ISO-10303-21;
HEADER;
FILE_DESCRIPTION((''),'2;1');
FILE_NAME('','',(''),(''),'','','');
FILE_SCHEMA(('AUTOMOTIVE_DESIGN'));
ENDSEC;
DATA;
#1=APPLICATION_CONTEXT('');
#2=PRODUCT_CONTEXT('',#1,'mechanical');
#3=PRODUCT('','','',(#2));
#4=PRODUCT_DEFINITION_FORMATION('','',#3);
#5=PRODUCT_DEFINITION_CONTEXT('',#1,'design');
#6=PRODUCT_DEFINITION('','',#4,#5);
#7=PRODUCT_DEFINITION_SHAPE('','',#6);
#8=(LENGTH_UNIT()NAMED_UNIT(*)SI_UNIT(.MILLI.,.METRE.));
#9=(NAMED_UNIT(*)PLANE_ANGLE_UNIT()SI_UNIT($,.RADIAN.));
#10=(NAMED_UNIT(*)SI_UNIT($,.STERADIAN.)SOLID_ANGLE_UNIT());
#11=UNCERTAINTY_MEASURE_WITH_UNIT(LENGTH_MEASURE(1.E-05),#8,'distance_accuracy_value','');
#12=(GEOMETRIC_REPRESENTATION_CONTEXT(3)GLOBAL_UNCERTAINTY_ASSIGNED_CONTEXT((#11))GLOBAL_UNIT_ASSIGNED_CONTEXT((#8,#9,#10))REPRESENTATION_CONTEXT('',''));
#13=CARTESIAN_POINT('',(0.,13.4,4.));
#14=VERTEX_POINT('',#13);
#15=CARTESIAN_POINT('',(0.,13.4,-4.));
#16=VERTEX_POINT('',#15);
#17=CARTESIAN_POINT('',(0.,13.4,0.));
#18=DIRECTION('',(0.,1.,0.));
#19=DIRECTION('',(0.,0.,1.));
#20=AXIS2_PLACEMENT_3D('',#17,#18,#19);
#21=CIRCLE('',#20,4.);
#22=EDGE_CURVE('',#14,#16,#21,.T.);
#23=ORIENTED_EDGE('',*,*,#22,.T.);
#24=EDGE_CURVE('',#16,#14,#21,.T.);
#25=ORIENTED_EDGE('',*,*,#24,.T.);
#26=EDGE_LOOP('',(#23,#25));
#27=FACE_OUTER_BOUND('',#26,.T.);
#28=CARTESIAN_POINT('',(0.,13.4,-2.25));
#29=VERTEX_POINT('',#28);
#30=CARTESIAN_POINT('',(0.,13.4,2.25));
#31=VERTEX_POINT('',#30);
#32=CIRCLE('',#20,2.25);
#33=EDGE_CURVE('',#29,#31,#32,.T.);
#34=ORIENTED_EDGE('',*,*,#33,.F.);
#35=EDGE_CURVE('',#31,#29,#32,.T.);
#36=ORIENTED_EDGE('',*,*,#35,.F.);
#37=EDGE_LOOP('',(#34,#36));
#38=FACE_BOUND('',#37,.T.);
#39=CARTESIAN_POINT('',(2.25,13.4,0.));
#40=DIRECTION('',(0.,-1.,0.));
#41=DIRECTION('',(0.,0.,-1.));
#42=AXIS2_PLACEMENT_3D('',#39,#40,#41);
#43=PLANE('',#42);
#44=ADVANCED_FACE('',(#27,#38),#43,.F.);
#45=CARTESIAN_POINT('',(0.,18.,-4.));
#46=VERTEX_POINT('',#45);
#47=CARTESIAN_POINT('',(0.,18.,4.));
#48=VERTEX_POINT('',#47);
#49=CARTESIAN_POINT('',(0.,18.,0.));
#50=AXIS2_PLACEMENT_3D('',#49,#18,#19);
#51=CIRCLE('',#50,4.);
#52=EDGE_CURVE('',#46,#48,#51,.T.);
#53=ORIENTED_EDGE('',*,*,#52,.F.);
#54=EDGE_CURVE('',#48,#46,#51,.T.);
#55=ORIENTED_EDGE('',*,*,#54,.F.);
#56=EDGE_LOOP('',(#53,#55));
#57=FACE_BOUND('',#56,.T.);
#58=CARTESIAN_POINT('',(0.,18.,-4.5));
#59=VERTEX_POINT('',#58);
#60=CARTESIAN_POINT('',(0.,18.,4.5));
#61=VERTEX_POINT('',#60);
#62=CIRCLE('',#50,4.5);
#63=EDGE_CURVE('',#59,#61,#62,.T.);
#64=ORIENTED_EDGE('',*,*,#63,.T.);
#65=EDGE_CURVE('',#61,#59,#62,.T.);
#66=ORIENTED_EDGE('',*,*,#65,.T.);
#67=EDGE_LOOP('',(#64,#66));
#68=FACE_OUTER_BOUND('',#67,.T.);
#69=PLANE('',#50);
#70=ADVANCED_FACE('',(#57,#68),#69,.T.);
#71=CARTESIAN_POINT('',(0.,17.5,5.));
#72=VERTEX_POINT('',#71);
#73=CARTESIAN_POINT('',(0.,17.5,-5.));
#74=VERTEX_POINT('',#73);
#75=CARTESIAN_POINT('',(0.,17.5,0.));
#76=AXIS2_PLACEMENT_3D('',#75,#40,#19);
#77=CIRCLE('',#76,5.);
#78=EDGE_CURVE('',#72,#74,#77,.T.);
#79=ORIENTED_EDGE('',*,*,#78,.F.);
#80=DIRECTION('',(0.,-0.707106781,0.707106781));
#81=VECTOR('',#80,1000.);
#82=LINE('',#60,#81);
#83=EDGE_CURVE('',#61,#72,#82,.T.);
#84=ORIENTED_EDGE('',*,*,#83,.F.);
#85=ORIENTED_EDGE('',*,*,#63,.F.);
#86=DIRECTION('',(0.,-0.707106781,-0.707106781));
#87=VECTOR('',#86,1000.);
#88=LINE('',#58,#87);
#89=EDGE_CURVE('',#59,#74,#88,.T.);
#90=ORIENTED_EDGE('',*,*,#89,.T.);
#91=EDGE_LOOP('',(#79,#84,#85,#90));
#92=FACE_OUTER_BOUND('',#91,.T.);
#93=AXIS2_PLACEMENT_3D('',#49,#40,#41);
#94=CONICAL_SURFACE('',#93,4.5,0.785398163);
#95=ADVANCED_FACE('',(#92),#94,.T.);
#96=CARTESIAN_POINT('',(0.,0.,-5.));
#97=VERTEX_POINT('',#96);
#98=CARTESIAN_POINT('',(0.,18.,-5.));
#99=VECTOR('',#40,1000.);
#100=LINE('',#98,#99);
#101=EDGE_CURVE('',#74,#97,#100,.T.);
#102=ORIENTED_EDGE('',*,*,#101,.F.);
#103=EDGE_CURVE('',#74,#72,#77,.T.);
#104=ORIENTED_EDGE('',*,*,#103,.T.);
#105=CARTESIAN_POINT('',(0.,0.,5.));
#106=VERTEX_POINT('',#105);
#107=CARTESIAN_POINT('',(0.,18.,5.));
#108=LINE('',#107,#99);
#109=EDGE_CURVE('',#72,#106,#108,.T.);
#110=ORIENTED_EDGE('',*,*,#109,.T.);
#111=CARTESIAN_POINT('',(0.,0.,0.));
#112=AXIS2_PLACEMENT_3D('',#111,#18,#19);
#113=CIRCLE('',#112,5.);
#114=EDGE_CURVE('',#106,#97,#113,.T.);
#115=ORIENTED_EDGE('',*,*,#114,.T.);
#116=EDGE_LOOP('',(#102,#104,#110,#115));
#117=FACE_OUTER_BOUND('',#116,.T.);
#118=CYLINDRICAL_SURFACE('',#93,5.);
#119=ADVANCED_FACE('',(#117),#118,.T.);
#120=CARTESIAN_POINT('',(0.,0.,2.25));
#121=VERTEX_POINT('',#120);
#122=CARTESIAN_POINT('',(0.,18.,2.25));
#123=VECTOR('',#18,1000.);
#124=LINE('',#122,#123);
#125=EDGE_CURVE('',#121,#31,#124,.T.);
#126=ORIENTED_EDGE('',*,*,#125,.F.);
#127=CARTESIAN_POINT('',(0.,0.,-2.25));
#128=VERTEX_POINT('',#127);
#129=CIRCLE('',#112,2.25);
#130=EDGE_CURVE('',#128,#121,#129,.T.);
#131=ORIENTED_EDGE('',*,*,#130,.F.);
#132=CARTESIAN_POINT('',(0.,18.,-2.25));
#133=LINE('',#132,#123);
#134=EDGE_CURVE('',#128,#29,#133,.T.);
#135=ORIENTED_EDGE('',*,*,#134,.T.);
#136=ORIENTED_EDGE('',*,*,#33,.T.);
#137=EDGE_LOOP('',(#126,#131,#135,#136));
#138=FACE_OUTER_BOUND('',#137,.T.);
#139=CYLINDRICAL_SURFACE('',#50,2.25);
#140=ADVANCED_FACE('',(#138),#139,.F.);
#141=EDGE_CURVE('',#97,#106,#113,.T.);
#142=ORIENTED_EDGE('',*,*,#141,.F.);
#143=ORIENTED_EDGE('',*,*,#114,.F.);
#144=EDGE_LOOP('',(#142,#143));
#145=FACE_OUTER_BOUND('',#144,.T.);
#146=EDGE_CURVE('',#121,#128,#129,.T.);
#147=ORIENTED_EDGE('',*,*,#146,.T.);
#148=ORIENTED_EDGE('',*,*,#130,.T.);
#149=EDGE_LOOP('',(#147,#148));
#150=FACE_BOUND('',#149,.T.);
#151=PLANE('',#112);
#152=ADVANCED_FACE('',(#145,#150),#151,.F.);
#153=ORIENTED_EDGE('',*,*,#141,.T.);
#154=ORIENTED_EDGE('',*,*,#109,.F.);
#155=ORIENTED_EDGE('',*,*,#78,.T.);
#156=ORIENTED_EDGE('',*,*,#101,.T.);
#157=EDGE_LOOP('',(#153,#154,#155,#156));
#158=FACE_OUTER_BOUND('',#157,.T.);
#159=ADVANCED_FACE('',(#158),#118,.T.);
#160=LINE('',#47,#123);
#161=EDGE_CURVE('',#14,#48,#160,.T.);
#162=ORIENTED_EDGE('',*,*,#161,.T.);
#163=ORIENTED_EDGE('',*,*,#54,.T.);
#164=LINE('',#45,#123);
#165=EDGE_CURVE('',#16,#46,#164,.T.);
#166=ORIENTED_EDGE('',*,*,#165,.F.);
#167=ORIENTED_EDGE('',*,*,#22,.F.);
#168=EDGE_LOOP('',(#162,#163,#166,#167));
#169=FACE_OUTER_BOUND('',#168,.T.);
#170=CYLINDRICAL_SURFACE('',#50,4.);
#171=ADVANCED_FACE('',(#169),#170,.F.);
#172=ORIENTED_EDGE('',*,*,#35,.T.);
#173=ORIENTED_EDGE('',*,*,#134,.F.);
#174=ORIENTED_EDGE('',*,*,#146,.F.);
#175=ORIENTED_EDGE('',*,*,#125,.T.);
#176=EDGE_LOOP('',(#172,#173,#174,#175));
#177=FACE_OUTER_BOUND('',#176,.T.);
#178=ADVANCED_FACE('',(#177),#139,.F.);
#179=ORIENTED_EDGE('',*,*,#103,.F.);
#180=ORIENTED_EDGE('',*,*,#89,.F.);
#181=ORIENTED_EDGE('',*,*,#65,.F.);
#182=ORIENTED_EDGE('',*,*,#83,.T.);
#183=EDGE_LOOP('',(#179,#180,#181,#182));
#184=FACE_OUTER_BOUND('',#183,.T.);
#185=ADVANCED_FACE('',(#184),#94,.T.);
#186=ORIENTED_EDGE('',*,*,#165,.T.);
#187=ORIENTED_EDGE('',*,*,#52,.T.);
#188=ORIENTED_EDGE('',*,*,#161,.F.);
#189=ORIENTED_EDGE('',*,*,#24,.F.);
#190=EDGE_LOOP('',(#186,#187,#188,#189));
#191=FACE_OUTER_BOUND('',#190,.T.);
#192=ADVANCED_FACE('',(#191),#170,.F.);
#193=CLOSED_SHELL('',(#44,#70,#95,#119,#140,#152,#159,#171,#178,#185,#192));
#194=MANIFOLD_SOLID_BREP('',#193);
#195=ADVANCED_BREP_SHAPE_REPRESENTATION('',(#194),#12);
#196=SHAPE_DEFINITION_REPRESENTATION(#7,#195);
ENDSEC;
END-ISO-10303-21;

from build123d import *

# Parameters (mm, degrees)
SKETCH1_R                                          = 5
BOSS_EXTRUDE1_DEPTH                                = 18
HOLE_WIZARD_SOCKET_HEAD_CAP_SCREW_TYPE_D           = 4.5
HOLE_WIZARD_SOCKET_HEAD_CAP_SCREW_TYPE_CBORE_D     = 8
HOLE_WIZARD_SOCKET_HEAD_CAP_SCREW_TYPE_CBORE_DEPTH = 4.6
CHAMFER1_SIZE                                      = 0.5


with BuildPart() as part:
    # Sketch1 → Boss-Extrude1 (new body)
    with BuildSketch(Plane(origin=(0, 0, 0), x_dir=(1, 0, 0), z_dir=(0, 1, 0))):
        with Locations(Location((0, 0, 0), (0, 0, 270))):
            Circle(SKETCH1_R)
    extrude(amount=BOSS_EXTRUDE1_DEPTH)

    # Hole wizard: socket head cap screw, type 1 (through all)
    with Locations(Plane(origin=(0, 18, 0), x_dir=(1, 0, 0), z_dir=(0, 1, 0))):
        with Locations((0, 0)):
            CounterBoreHole(HOLE_WIZARD_SOCKET_HEAD_CAP_SCREW_TYPE_D / 2, HOLE_WIZARD_SOCKET_HEAD_CAP_SCREW_TYPE_CBORE_D / 2, HOLE_WIZARD_SOCKET_HEAD_CAP_SCREW_TYPE_CBORE_DEPTH)

    # Chamfer1
    chamfer1_edges = [part.edges().sort_by_distance(p)[0] for p in [
        (0, 18, -5),
    ]]
    chamfer(chamfer1_edges, length=CHAMFER1_SIZE)


solid = part.part
